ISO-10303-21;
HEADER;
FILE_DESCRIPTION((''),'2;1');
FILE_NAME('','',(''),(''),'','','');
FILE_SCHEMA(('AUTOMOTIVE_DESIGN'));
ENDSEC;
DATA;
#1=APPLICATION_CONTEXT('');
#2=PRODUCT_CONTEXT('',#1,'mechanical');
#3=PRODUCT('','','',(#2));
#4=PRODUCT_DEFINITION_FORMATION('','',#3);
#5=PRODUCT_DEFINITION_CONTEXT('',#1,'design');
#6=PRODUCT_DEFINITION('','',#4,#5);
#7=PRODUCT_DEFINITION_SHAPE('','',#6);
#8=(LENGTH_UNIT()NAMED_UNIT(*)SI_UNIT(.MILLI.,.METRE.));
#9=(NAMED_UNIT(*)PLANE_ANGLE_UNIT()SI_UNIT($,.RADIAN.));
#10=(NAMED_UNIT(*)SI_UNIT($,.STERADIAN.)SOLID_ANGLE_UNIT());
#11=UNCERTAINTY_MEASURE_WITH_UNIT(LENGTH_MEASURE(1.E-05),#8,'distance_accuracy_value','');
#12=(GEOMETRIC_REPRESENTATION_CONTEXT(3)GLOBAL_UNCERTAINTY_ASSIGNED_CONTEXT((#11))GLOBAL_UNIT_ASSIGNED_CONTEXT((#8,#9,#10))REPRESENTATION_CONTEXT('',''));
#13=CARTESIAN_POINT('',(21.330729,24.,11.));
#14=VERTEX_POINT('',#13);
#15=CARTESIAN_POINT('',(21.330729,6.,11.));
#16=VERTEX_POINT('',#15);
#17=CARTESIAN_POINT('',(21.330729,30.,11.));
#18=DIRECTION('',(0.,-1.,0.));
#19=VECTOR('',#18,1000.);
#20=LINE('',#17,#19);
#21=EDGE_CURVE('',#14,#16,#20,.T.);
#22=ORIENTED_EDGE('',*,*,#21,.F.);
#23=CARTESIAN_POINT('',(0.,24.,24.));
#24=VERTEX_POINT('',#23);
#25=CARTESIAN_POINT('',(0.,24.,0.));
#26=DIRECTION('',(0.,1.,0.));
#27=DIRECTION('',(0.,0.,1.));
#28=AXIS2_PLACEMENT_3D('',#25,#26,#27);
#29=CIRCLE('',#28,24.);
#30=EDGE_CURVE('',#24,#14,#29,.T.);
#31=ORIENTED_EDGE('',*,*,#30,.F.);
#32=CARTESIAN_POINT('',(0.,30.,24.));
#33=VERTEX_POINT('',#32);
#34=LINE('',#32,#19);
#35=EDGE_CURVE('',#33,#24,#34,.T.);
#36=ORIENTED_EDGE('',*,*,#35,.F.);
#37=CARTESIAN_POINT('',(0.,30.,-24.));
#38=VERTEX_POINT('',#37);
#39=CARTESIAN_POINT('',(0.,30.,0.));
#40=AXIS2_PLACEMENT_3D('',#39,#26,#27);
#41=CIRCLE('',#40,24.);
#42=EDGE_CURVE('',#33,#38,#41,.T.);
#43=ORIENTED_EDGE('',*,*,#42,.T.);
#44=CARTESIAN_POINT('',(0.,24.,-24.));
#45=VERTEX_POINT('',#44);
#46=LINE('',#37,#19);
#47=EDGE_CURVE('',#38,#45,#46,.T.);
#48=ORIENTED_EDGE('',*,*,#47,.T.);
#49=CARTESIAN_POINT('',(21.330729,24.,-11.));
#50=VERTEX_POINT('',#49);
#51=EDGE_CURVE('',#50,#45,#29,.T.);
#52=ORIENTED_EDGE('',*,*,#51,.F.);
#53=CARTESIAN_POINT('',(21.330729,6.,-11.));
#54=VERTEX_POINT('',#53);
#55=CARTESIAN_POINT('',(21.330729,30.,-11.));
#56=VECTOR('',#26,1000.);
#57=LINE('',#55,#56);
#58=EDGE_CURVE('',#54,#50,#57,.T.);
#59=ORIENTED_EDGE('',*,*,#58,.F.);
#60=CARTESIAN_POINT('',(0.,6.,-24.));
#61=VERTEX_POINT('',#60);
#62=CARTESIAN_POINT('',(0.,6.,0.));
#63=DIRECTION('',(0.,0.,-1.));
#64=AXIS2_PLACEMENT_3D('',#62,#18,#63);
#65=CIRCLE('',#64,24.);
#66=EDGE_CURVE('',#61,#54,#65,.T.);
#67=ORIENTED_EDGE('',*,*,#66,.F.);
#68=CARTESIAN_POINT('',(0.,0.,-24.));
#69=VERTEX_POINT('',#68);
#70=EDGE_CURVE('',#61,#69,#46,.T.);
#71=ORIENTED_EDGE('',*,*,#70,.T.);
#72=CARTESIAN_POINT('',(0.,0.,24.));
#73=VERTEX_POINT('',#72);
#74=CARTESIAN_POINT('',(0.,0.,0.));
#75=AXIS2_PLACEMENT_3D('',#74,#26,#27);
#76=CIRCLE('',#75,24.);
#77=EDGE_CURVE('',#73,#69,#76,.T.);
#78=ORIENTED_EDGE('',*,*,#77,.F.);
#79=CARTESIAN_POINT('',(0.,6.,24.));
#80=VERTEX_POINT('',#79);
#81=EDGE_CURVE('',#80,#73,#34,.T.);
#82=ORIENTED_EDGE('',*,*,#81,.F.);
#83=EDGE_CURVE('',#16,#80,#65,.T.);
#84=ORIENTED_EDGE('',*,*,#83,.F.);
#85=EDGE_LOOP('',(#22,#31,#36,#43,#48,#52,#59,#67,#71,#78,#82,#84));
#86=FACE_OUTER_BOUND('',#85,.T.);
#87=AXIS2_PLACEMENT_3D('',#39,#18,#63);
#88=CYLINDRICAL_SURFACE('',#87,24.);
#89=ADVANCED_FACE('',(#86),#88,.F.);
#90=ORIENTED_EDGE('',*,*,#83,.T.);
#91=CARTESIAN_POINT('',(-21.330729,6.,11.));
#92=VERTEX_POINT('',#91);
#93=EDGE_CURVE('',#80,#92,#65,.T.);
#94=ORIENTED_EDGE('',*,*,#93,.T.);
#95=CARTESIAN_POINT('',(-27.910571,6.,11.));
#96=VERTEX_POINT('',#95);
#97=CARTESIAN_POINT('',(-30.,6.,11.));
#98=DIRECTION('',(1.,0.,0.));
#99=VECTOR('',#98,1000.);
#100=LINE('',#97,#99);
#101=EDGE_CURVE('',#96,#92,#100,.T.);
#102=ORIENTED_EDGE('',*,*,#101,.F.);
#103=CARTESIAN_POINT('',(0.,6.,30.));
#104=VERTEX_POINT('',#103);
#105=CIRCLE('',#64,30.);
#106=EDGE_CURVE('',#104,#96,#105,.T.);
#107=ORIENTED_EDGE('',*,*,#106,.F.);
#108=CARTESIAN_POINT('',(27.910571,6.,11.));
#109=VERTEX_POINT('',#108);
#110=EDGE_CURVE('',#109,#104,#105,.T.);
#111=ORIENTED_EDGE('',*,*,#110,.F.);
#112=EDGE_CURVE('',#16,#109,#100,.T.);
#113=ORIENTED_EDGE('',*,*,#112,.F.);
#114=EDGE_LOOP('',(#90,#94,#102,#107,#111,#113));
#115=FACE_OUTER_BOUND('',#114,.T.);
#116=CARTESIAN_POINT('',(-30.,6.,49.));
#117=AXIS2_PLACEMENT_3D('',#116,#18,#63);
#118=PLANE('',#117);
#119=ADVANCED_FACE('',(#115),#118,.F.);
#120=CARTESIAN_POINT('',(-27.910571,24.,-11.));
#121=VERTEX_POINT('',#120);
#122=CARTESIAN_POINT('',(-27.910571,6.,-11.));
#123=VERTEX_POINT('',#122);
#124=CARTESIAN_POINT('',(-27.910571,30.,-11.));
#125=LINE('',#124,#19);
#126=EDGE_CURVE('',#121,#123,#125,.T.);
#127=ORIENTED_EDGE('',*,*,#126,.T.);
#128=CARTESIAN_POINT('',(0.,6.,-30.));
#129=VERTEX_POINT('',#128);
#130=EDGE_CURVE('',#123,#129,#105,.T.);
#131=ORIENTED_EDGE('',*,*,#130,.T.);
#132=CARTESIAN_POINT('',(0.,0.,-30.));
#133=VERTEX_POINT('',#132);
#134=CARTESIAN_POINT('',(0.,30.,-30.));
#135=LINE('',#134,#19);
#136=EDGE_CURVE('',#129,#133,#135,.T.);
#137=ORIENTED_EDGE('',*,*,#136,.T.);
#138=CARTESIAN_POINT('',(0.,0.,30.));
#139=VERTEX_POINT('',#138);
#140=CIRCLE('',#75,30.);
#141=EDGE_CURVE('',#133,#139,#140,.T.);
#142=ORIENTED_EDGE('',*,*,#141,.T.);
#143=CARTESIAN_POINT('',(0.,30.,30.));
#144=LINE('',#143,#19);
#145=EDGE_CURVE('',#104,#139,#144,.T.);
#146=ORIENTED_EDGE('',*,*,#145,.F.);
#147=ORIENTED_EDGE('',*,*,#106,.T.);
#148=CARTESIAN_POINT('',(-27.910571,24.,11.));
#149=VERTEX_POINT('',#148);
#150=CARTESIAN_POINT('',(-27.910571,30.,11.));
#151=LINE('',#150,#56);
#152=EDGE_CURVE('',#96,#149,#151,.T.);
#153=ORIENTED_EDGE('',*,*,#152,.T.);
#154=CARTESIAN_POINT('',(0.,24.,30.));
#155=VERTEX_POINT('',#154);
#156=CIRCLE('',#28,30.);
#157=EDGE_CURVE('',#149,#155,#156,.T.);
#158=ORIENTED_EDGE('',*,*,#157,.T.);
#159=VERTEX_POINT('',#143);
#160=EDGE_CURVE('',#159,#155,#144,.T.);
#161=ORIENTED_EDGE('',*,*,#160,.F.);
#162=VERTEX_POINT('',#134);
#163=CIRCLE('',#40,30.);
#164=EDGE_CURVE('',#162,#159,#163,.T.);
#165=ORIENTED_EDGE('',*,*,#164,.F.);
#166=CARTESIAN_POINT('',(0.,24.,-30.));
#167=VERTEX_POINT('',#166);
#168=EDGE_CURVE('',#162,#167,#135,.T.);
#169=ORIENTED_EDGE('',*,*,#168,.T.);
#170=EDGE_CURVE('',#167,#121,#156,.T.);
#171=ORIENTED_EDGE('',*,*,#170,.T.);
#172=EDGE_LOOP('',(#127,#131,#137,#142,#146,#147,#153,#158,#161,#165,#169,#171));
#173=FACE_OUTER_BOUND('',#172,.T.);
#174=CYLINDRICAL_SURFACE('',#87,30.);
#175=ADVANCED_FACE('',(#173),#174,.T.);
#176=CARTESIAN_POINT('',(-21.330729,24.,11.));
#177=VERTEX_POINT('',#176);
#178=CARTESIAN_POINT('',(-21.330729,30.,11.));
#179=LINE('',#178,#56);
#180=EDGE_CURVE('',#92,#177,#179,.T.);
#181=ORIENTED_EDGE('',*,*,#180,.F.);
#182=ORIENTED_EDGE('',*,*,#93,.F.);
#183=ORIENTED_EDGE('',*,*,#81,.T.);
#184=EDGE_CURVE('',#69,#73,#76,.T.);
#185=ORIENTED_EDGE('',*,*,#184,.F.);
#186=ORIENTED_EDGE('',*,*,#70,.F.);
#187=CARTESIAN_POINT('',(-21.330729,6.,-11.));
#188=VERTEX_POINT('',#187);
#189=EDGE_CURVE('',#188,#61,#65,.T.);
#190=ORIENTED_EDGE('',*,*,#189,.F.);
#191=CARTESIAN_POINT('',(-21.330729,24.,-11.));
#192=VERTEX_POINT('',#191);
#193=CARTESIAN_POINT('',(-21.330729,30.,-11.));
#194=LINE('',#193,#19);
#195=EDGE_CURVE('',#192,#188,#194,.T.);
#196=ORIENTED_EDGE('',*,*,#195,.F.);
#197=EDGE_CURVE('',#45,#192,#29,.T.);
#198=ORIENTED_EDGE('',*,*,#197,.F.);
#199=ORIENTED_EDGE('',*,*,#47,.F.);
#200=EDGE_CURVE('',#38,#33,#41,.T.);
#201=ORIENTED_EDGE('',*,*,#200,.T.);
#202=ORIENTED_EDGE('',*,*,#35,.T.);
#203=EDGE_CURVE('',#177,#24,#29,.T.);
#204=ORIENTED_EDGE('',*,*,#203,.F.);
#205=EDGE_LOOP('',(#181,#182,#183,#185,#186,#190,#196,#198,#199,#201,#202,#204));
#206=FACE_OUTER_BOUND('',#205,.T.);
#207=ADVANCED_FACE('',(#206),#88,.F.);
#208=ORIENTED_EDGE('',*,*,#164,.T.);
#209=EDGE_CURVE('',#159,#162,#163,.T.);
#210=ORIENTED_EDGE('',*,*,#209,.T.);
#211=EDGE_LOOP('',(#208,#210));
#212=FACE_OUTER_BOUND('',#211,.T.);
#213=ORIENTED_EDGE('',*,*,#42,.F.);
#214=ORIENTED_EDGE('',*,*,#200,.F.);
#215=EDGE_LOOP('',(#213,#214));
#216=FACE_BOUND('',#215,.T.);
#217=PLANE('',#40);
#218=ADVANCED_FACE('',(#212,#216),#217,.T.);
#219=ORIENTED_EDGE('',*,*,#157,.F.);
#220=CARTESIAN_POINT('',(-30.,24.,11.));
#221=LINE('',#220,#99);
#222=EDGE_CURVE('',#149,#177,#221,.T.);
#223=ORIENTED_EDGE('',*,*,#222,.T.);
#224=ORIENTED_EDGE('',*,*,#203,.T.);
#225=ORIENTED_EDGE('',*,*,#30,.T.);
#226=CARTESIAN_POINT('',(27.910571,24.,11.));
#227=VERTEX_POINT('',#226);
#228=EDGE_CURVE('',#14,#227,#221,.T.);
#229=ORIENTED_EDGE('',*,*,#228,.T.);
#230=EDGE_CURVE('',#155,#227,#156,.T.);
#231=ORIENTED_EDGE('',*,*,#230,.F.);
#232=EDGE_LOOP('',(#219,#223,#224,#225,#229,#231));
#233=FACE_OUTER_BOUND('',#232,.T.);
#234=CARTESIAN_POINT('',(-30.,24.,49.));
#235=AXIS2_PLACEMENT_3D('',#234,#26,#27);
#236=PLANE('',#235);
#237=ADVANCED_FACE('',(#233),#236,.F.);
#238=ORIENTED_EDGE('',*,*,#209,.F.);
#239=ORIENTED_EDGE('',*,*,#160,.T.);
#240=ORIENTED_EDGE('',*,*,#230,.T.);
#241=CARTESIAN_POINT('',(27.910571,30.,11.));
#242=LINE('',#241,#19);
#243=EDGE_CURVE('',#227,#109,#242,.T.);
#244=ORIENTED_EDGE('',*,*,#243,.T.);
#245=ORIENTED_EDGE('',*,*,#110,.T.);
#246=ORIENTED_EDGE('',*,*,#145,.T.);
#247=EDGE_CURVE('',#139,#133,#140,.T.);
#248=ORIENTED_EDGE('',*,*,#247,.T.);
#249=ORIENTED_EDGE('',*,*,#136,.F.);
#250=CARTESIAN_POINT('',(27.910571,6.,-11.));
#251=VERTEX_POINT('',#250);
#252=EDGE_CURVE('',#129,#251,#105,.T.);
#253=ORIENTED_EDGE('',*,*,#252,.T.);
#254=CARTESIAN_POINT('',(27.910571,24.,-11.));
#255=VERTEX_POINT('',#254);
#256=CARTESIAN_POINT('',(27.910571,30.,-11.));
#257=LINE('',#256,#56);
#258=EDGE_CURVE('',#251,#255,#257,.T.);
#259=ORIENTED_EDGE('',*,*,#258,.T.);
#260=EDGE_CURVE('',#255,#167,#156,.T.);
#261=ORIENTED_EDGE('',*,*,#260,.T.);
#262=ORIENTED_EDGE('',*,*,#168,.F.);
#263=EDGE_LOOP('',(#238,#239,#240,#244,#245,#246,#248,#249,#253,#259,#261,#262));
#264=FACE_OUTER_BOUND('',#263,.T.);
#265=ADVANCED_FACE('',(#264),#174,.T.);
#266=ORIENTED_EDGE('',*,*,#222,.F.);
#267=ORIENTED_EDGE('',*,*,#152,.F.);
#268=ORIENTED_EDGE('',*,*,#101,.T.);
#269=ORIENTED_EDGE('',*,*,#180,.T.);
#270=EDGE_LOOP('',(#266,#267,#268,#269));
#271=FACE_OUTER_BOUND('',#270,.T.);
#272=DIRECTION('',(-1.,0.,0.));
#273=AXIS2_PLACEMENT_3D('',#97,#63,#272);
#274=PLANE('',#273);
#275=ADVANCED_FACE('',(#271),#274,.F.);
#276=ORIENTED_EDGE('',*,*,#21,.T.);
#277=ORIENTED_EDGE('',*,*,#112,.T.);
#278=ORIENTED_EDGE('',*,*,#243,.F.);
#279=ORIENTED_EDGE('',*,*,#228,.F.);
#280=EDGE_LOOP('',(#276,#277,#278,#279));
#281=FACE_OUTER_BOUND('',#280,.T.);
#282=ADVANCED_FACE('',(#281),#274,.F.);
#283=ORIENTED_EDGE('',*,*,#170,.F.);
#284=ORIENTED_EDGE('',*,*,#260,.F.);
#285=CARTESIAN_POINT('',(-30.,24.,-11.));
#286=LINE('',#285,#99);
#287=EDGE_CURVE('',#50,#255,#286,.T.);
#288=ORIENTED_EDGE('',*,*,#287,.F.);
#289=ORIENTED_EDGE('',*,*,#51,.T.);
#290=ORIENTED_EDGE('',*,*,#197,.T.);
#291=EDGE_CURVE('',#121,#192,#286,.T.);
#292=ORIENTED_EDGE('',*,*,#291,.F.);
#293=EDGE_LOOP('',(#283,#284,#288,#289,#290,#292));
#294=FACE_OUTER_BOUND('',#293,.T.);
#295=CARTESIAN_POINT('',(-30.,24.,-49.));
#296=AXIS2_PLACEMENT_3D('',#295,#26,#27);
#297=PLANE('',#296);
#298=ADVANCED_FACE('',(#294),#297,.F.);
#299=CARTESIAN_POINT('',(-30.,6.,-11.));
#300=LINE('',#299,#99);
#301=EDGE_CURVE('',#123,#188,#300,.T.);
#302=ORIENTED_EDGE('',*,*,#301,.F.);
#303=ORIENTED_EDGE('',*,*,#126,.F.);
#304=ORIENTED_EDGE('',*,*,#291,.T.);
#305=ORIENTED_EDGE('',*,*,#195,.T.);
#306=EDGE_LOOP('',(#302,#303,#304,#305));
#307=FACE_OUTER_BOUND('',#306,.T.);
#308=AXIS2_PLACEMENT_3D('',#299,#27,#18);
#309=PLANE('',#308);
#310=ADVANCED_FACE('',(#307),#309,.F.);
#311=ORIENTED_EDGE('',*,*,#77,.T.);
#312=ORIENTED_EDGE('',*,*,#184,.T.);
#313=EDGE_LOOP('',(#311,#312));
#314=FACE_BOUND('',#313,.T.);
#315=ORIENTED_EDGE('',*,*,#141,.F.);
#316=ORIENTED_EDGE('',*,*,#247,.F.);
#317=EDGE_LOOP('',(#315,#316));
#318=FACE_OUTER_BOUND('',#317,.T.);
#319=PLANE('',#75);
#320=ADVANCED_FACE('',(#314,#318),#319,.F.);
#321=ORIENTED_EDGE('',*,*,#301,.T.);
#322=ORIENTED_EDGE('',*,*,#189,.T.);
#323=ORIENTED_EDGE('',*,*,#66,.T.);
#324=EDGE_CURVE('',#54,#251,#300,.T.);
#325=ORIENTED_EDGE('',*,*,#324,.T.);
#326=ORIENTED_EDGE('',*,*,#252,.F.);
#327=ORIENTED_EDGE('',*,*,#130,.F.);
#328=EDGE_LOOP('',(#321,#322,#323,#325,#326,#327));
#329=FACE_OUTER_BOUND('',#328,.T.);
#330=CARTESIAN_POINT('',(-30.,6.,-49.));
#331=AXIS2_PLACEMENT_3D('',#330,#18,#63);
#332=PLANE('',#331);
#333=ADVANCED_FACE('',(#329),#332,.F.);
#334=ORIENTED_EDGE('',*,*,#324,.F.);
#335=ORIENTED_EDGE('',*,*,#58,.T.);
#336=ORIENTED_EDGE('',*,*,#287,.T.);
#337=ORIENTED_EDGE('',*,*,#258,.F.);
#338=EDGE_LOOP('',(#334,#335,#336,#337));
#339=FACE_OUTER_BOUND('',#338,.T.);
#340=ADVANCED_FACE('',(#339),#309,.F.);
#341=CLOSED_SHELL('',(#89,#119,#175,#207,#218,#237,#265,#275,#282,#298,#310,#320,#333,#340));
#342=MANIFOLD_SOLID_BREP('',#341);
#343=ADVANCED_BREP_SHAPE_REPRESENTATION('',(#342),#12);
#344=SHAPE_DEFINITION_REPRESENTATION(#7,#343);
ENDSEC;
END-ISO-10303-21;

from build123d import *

# Parameters (mm, degrees)
SKETCH1_R               = 30
SKETCH1_R_2             = 24
BOSS_EXTRUDE1_DEPTH     = 30
CUT_EXTRUDE1_DEPTH      = 52.961524227
CUT_EXTRUDE1_DEPTH_BACK = 52.961524227
SKETCH2_W               = 38
SKETCH2_H               = 18


with BuildPart() as part:
    # Sketch1 → Boss-Extrude1 (new body)
    with BuildSketch(Plane(origin=(0, 0, 0), x_dir=(1, 0, 0), z_dir=(0, 1, 0))):
        with Locations(Location((0, 0, 0), (0, 0, 270))):
            Circle(SKETCH1_R)
        with Locations(Location((0, 0, 0), (0, 0, 270))):
            Circle(SKETCH1_R_2, mode=Mode.SUBTRACT)
    extrude(amount=BOSS_EXTRUDE1_DEPTH)

    # Sketch2 → Cut-Extrude1 (cut, two sides: drawn at the far end of the back side and taken through both)
    with BuildSketch(Plane(origin=(0, 0, 0), x_dir=(0, 0, -1), z_dir=(1, 0, 0)).offset(-CUT_EXTRUDE1_DEPTH_BACK)):
        with Locations((-30, 15)):
            Rectangle(SKETCH2_W, SKETCH2_H)
        with Locations((30, 15)):
            Rectangle(SKETCH2_W, SKETCH2_H)
    extrude(amount=CUT_EXTRUDE1_DEPTH + CUT_EXTRUDE1_DEPTH_BACK, mode=Mode.SUBTRACT)


solid = part.part
